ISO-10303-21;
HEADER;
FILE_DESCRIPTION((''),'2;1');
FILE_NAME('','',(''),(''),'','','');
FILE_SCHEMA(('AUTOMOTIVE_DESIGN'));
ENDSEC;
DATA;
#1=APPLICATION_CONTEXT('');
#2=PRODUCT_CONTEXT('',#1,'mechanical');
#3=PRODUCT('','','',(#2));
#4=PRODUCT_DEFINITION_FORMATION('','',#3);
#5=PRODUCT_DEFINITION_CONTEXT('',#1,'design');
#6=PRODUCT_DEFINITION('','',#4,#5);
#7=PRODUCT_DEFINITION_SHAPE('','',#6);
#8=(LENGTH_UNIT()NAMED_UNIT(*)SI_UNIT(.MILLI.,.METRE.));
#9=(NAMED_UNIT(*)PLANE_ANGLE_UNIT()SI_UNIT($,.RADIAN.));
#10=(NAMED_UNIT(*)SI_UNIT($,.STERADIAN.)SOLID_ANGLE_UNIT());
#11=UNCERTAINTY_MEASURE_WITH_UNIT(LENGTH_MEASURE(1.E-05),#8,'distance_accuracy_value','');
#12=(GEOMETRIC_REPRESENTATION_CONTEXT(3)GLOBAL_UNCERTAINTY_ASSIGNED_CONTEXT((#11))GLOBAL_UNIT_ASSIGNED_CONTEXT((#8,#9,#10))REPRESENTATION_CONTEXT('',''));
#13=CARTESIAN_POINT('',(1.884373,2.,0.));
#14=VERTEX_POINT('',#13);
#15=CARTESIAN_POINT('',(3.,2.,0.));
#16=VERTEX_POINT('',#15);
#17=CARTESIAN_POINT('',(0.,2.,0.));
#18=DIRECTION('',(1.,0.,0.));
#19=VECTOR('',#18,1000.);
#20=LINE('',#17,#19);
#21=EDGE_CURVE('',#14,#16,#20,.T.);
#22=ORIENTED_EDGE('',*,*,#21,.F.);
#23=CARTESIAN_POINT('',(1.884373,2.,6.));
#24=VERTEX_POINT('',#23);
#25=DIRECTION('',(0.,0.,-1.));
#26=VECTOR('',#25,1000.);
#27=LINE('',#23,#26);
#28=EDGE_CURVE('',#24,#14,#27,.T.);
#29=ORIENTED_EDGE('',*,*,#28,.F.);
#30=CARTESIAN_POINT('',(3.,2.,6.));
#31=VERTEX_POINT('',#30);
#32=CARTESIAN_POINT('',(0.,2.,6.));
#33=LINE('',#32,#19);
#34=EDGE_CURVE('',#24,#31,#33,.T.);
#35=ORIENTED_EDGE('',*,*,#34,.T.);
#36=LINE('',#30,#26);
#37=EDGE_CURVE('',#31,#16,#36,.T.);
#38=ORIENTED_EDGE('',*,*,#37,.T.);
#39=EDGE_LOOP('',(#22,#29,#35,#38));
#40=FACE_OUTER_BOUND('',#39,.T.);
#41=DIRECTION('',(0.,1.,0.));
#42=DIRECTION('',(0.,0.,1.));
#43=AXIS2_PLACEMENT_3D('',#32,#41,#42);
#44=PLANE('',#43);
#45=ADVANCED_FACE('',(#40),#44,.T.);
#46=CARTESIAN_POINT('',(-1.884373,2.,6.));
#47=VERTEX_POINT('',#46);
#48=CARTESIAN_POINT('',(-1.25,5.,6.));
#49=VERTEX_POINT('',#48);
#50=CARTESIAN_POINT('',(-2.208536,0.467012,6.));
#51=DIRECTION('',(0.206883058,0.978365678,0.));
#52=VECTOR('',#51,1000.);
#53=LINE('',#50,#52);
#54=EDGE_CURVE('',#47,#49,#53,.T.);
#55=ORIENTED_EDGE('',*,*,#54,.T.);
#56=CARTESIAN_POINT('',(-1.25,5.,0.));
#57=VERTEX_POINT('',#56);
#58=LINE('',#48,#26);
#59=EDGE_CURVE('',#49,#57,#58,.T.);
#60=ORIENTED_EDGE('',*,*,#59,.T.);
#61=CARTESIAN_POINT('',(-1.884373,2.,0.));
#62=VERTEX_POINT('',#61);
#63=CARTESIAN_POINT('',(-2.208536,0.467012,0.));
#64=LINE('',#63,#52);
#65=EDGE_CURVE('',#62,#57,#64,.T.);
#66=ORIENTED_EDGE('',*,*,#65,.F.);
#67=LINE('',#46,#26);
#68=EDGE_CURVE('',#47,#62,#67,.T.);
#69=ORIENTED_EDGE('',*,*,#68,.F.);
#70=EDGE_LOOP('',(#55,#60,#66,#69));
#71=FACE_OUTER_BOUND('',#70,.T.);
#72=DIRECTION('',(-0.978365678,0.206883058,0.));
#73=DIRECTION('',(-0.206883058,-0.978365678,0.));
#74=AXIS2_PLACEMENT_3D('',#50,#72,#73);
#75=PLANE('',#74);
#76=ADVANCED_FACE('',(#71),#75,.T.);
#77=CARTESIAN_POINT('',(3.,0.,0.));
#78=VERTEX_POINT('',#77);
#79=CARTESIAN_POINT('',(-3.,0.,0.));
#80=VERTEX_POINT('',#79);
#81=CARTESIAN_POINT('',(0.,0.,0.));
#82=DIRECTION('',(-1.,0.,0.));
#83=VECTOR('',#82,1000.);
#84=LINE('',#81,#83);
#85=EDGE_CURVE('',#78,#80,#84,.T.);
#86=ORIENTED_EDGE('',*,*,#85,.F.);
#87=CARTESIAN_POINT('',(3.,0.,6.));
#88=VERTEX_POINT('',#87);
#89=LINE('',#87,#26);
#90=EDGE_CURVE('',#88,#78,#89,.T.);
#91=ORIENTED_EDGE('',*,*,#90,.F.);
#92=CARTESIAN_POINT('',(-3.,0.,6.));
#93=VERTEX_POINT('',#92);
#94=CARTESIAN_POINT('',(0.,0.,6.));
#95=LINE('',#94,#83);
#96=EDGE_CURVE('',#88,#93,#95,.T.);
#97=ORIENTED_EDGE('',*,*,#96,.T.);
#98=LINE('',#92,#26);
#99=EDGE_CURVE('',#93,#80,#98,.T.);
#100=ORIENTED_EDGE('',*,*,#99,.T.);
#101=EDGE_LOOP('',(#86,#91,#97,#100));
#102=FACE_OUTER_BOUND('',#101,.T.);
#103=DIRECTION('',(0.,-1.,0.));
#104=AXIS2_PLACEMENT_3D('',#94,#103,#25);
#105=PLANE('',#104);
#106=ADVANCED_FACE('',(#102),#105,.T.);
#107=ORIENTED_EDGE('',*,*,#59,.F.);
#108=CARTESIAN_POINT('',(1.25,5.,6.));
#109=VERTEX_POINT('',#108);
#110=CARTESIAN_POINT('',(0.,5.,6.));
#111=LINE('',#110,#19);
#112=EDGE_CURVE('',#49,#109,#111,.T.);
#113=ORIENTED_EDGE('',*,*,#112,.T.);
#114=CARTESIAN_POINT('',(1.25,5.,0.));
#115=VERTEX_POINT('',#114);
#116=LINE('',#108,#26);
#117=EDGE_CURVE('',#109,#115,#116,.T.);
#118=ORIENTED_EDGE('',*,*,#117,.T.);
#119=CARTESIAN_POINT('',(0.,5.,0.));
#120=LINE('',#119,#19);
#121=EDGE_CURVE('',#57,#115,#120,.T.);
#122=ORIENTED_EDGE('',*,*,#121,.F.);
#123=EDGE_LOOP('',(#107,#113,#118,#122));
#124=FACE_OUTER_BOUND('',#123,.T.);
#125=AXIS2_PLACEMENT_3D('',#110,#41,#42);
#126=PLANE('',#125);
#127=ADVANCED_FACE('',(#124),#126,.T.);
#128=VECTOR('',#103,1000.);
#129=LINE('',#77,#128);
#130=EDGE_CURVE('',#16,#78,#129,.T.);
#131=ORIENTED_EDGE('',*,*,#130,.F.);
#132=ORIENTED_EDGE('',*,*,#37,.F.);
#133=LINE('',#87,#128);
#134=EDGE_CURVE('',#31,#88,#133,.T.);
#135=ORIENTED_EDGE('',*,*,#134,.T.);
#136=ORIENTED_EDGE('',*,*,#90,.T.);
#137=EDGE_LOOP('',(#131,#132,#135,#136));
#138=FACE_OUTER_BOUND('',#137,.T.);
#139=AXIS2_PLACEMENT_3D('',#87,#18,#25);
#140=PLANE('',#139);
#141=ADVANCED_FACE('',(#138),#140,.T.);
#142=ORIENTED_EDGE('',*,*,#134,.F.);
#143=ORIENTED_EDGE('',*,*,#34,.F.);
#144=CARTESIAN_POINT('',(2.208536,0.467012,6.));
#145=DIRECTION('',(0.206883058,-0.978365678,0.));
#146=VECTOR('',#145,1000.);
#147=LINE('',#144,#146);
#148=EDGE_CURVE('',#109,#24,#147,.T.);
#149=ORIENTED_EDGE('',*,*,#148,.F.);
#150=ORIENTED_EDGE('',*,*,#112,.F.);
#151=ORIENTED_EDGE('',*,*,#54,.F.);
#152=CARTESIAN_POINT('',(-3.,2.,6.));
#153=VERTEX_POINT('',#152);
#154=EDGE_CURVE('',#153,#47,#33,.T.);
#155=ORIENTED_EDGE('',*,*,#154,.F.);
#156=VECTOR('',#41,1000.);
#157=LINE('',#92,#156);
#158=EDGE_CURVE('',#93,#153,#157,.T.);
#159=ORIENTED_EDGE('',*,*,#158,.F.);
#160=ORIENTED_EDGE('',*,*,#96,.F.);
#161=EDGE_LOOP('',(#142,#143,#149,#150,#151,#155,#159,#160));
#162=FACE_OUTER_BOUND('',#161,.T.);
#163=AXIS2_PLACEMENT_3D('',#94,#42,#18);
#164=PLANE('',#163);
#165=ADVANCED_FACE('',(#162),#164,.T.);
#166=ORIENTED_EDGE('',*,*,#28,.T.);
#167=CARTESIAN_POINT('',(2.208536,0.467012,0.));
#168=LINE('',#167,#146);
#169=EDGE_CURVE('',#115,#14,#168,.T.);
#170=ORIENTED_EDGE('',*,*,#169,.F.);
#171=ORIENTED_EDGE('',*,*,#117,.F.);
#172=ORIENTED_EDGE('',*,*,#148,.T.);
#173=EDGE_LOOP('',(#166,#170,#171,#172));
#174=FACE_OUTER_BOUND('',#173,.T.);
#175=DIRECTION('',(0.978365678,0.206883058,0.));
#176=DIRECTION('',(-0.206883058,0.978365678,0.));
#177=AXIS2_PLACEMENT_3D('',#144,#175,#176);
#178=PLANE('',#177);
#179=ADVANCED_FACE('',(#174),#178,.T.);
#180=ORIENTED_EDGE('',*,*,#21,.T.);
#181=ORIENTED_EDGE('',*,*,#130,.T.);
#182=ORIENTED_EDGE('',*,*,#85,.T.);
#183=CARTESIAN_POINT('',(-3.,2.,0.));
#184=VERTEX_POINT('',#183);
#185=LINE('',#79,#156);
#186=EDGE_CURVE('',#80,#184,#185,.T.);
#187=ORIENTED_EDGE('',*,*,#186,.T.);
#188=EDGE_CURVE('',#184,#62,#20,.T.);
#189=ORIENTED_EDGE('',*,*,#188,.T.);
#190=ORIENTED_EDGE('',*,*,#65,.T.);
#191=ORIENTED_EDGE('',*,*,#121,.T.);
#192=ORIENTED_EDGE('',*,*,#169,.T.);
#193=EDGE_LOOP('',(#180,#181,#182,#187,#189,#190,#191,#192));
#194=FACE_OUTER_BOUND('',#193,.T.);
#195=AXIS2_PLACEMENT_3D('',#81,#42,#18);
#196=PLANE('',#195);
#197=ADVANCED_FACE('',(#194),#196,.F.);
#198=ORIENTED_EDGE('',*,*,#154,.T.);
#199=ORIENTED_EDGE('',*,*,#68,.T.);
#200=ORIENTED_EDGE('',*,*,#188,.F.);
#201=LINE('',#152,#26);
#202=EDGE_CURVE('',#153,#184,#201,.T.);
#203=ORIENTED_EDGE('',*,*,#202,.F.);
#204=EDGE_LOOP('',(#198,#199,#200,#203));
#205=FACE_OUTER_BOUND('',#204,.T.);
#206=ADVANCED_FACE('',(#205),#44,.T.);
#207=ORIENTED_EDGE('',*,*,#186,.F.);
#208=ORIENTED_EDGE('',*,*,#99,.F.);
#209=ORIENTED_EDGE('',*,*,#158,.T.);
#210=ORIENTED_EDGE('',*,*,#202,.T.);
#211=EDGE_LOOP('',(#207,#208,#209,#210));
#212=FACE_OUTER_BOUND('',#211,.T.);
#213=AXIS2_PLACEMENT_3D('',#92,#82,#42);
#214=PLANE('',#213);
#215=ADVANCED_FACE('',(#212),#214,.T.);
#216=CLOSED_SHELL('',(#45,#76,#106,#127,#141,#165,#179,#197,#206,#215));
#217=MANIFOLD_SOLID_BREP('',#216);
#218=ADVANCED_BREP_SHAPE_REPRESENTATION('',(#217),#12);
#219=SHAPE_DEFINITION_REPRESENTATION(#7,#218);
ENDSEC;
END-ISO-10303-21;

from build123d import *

# Parameters (mm, degrees)
BOSS_EXTRUDE1_DEPTH = 6


with BuildPart() as part:
    # Sketch1 → Boss-Extrude1 (new body)
    with BuildSketch(Plane.XY):
        Polygon((-3, 0), (0, 0), (0, 5), (-1.25, 5), (-1.884373414, 2), (-3, 2), align=None)
        Polygon((0, 5), (0, 0), (3, 0), (3, 2), (1.884373414, 2), (1.25, 5), align=None)
    extrude(amount=BOSS_EXTRUDE1_DEPTH)


solid = part.part
